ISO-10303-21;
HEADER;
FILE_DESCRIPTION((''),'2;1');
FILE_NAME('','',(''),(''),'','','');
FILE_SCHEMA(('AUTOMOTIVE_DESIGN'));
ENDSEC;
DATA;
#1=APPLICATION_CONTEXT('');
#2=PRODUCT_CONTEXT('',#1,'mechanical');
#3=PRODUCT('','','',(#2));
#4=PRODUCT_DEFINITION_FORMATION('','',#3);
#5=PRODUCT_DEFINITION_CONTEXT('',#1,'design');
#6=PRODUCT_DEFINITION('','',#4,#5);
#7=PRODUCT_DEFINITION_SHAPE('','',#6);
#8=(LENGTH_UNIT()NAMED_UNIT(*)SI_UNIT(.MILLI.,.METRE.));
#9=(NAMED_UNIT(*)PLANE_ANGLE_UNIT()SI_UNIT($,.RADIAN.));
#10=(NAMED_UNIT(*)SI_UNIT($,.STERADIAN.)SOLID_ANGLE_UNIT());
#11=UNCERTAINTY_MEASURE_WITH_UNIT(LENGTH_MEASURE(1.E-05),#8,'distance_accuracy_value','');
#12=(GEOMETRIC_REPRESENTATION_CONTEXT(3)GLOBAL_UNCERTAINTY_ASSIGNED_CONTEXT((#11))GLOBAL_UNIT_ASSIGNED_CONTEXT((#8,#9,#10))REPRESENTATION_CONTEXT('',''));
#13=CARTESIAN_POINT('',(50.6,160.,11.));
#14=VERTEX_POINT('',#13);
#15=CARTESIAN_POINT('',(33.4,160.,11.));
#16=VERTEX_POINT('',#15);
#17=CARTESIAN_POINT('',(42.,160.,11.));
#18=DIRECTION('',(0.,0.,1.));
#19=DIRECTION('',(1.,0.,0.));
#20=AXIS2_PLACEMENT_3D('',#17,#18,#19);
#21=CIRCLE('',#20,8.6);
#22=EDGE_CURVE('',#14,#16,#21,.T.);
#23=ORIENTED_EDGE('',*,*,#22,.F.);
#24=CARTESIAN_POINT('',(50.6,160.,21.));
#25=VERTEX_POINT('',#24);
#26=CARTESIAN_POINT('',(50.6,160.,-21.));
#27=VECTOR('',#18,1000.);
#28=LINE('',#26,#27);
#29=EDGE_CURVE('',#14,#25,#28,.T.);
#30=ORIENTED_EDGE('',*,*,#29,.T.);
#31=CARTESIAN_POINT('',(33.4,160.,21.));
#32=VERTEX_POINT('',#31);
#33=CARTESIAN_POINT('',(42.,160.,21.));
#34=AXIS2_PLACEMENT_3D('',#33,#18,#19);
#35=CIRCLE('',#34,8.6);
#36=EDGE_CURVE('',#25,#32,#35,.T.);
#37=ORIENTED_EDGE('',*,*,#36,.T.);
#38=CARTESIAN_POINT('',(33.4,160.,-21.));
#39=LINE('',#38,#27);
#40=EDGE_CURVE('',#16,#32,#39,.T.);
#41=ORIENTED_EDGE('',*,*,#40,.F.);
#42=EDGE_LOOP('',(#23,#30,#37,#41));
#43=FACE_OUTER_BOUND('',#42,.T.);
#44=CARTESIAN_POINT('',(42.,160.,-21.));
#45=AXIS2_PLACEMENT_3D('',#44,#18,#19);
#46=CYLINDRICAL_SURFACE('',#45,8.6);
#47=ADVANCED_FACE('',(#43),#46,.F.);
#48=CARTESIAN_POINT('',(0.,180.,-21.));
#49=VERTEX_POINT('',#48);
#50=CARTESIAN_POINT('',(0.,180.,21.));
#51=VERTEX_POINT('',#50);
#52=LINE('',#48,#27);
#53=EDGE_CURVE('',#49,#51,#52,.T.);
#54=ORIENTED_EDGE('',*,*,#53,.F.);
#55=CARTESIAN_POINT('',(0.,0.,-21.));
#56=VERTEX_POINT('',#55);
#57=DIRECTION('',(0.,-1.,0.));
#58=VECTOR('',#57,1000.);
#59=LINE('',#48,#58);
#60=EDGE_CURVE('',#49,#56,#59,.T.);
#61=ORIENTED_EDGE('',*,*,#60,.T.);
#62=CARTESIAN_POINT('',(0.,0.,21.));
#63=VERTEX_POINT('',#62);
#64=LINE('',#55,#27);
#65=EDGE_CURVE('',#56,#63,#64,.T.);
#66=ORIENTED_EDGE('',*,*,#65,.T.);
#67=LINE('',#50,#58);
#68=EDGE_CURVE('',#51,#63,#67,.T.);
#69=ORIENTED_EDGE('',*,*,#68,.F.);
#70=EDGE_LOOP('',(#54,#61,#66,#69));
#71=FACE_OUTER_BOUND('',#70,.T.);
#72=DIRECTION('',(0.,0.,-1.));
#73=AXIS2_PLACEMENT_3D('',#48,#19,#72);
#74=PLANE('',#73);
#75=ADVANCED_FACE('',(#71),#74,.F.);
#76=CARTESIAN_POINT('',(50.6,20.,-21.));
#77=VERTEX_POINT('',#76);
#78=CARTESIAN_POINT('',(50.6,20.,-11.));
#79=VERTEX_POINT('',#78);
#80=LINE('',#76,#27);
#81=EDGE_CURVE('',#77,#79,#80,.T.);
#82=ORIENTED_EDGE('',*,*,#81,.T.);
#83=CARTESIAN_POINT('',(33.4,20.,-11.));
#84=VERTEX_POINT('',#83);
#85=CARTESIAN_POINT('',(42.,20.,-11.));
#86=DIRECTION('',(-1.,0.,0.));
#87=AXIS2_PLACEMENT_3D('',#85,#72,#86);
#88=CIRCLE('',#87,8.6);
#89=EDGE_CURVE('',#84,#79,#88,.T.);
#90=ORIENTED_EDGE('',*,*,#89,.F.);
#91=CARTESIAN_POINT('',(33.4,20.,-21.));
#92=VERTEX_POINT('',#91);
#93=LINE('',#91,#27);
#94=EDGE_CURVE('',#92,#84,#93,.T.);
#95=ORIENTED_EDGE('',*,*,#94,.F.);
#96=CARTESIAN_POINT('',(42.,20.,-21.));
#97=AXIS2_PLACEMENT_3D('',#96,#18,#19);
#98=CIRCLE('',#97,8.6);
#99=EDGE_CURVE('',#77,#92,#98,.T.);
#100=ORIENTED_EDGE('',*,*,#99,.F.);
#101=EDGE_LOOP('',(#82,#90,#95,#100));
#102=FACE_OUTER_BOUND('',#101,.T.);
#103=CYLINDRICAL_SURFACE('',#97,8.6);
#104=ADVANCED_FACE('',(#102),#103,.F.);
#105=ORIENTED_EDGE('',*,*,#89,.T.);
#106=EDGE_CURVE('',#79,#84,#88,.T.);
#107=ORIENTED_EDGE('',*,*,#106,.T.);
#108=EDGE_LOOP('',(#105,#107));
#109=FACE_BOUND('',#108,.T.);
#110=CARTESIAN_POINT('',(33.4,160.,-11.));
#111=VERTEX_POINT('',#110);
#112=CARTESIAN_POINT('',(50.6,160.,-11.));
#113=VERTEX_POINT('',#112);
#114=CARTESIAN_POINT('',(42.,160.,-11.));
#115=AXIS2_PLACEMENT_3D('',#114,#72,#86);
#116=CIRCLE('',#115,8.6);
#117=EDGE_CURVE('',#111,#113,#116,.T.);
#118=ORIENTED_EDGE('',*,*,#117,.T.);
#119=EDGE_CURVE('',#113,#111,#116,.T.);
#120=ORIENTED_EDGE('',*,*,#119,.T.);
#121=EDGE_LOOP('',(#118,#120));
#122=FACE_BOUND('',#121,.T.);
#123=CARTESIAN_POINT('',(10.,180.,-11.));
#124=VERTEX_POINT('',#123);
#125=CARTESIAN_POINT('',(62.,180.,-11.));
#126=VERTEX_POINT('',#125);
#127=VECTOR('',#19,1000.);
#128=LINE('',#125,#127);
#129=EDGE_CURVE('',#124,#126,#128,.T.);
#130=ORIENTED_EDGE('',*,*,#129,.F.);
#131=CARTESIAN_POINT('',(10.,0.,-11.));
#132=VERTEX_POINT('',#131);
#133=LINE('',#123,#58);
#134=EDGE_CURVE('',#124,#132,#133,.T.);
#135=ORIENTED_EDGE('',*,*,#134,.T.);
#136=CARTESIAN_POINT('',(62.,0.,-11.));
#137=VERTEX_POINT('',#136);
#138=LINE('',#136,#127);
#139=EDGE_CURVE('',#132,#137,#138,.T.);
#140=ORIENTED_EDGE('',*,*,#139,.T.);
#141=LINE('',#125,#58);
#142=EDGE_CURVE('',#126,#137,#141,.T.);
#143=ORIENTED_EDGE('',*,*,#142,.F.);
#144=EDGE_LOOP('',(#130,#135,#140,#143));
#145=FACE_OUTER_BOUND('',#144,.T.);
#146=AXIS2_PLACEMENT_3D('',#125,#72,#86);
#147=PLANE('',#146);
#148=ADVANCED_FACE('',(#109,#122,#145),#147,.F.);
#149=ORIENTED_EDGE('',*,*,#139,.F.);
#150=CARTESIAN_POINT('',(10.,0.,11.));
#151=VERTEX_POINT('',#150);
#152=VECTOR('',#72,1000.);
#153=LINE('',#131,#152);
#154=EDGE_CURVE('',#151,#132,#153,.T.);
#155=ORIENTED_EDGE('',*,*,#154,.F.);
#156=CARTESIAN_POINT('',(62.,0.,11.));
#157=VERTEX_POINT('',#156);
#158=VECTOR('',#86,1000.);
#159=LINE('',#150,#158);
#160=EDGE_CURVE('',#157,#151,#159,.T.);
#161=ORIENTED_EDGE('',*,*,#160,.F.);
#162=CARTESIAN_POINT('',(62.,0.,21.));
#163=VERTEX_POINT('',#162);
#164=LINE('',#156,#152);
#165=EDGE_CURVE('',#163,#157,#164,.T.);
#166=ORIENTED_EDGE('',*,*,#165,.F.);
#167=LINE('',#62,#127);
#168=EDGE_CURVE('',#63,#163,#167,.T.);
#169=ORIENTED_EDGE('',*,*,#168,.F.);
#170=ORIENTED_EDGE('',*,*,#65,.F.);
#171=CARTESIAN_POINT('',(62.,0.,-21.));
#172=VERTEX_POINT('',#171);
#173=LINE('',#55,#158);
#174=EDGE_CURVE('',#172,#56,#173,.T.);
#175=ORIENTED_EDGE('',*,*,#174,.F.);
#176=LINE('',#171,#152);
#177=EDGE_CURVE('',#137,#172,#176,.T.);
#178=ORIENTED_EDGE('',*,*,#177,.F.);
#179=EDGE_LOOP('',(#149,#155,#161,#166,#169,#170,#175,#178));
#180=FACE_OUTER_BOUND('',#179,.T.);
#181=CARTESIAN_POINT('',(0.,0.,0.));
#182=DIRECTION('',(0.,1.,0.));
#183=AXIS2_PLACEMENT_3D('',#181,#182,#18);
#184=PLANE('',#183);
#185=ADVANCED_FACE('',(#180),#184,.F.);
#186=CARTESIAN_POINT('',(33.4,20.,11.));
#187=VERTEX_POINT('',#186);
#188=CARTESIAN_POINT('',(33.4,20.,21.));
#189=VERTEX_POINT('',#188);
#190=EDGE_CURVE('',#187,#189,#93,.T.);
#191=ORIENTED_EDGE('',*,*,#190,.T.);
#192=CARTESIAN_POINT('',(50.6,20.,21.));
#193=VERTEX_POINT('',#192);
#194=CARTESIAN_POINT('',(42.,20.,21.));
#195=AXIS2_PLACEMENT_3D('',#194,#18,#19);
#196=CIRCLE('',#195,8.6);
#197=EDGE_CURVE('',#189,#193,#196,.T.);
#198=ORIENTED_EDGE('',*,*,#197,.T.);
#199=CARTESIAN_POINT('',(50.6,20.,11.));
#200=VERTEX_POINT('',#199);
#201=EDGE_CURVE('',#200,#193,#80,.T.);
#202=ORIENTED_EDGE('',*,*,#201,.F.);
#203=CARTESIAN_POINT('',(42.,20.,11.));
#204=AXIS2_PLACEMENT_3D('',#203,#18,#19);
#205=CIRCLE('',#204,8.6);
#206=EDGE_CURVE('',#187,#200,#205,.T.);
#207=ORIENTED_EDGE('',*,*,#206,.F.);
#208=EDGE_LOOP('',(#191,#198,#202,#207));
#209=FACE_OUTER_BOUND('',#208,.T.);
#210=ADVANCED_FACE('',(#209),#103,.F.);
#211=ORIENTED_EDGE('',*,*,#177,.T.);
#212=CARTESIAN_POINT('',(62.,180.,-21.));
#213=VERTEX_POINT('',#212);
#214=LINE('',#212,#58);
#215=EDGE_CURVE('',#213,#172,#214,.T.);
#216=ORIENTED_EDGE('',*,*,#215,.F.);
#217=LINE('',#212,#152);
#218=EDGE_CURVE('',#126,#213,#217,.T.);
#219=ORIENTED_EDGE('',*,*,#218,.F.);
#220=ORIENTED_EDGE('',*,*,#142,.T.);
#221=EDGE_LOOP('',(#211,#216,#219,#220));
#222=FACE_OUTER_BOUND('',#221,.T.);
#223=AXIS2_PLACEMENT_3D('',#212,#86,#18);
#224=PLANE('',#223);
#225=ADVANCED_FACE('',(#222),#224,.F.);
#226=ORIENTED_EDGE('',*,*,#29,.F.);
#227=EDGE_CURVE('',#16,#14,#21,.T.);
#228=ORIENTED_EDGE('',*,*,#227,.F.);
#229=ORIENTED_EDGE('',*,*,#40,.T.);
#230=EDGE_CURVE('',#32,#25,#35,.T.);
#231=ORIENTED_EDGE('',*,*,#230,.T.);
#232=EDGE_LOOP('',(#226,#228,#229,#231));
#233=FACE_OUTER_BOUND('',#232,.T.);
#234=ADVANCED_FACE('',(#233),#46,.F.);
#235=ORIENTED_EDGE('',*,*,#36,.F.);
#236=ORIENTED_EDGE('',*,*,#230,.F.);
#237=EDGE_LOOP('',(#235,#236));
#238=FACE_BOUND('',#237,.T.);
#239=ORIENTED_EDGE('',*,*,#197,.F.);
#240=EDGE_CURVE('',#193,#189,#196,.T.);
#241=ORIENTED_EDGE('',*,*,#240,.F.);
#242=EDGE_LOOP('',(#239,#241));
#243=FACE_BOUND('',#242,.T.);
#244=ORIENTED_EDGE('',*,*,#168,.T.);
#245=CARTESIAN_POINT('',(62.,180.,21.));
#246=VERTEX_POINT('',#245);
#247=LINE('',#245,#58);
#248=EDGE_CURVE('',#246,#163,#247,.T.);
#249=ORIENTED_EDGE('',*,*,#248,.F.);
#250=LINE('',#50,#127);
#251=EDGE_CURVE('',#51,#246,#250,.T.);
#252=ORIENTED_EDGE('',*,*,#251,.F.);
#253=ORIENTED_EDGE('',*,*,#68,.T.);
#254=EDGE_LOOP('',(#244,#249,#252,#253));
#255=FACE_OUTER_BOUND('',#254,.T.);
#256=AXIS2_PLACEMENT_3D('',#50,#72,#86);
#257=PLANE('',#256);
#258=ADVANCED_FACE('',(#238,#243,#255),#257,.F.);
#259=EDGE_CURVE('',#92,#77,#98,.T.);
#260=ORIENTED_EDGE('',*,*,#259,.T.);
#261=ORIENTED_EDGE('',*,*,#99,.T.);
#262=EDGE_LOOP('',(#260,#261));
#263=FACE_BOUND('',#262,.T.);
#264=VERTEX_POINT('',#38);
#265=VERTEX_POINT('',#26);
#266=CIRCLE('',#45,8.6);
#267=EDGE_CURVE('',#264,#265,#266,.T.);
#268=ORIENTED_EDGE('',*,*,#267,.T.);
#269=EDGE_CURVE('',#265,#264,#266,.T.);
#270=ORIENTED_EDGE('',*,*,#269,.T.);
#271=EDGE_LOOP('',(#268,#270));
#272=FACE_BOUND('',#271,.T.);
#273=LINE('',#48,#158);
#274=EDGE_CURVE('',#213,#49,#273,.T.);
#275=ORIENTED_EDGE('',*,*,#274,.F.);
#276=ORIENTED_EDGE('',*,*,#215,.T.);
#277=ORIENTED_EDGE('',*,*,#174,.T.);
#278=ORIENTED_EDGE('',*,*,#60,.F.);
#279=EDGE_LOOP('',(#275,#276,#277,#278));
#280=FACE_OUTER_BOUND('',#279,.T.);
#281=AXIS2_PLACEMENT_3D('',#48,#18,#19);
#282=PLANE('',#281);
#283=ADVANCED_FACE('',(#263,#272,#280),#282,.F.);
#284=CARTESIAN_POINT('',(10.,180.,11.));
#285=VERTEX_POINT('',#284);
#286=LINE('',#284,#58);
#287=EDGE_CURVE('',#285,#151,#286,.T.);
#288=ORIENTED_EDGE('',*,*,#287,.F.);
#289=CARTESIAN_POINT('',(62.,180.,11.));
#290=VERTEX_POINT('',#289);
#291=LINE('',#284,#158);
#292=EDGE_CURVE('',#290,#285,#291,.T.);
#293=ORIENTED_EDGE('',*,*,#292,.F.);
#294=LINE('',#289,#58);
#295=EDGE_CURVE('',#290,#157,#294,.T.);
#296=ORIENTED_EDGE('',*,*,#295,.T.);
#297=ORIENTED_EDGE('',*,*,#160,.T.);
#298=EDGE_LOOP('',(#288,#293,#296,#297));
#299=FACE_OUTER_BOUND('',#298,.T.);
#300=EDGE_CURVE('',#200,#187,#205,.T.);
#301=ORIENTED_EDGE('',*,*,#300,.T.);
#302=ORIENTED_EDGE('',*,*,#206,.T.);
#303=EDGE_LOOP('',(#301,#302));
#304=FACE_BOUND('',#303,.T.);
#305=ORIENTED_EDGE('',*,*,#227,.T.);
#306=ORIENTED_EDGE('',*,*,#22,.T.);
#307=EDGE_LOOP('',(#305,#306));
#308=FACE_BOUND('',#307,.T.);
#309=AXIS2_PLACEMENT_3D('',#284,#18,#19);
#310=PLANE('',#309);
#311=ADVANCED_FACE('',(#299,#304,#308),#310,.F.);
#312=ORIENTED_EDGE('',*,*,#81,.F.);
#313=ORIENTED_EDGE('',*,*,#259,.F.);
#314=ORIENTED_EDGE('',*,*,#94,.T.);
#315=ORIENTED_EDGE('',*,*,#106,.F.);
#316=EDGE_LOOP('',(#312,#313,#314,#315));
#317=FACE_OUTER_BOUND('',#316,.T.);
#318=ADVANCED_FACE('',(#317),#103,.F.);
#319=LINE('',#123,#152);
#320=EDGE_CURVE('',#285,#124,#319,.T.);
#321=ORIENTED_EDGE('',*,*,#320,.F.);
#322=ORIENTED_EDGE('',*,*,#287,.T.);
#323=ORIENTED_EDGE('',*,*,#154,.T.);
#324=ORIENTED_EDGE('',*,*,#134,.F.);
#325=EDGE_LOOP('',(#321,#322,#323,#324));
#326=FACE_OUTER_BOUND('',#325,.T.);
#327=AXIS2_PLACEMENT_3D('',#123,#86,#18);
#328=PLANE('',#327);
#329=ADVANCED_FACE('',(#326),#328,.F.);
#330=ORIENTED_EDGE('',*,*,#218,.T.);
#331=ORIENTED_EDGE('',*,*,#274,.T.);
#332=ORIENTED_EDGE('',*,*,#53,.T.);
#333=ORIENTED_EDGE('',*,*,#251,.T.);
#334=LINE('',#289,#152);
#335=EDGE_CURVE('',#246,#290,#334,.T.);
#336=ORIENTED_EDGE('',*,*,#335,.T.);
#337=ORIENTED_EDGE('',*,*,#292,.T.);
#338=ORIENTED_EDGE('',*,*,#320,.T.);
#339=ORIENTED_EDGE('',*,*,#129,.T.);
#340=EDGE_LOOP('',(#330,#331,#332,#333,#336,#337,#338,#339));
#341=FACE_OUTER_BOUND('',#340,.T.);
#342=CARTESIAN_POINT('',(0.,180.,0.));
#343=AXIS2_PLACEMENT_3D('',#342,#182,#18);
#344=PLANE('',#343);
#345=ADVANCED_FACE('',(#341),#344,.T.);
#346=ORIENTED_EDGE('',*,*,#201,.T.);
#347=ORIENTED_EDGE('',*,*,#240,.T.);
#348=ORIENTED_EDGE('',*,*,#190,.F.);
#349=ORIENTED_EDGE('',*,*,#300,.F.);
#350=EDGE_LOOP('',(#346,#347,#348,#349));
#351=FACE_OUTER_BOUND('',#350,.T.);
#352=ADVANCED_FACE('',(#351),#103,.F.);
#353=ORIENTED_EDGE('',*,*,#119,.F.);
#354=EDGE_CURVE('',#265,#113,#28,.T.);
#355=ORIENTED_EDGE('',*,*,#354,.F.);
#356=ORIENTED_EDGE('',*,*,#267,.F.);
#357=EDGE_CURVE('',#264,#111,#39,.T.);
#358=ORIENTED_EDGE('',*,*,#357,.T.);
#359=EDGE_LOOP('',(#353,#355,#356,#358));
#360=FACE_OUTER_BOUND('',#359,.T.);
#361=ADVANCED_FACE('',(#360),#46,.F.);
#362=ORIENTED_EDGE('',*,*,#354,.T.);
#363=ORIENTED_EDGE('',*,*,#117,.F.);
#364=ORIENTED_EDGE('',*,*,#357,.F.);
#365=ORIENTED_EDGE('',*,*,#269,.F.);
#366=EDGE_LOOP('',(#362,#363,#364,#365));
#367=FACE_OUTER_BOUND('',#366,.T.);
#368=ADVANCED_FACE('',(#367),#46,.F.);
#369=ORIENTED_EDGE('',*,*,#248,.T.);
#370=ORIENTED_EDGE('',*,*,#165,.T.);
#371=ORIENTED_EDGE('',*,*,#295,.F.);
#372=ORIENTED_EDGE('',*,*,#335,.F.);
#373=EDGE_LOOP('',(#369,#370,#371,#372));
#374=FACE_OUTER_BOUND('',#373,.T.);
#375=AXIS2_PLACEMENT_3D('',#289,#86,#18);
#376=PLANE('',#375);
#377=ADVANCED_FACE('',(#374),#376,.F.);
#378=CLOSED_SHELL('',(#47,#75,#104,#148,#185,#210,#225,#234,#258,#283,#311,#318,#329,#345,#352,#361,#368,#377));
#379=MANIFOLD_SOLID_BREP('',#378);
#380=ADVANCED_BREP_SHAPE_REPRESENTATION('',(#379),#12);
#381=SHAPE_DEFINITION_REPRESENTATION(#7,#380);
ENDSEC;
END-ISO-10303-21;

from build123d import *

# Parameters (mm, degrees)
EXTRUDE_1_DEPTH     = 180
SKETCH_2_R          = 8.6
CUT_EXTRUDE_1_DEPTH = 195.956405383


with BuildPart() as part:
    # 草图1 → 凸台-拉伸1 (new body)
    with BuildSketch(Plane(origin=(0, 0, 0), x_dir=(1, 0, 0), z_dir=(0, 1, 0))):
        Polygon((62, 11), (10, 11), (10, -11), (62, -11), (62, -21), (0, -21), (0, 21), (62, 21), align=None)
    extrude(amount=EXTRUDE_1_DEPTH)

    # 草图2 → 切除-拉伸1 (cut, through all)
    with BuildSketch(Plane.XY.offset(21)):
        with Locations((42, 160)):
            Circle(SKETCH_2_R)
        with Locations((42, 20)):
            Circle(SKETCH_2_R)
    extrude(amount=-CUT_EXTRUDE_1_DEPTH, mode=Mode.SUBTRACT)


solid = part.part
